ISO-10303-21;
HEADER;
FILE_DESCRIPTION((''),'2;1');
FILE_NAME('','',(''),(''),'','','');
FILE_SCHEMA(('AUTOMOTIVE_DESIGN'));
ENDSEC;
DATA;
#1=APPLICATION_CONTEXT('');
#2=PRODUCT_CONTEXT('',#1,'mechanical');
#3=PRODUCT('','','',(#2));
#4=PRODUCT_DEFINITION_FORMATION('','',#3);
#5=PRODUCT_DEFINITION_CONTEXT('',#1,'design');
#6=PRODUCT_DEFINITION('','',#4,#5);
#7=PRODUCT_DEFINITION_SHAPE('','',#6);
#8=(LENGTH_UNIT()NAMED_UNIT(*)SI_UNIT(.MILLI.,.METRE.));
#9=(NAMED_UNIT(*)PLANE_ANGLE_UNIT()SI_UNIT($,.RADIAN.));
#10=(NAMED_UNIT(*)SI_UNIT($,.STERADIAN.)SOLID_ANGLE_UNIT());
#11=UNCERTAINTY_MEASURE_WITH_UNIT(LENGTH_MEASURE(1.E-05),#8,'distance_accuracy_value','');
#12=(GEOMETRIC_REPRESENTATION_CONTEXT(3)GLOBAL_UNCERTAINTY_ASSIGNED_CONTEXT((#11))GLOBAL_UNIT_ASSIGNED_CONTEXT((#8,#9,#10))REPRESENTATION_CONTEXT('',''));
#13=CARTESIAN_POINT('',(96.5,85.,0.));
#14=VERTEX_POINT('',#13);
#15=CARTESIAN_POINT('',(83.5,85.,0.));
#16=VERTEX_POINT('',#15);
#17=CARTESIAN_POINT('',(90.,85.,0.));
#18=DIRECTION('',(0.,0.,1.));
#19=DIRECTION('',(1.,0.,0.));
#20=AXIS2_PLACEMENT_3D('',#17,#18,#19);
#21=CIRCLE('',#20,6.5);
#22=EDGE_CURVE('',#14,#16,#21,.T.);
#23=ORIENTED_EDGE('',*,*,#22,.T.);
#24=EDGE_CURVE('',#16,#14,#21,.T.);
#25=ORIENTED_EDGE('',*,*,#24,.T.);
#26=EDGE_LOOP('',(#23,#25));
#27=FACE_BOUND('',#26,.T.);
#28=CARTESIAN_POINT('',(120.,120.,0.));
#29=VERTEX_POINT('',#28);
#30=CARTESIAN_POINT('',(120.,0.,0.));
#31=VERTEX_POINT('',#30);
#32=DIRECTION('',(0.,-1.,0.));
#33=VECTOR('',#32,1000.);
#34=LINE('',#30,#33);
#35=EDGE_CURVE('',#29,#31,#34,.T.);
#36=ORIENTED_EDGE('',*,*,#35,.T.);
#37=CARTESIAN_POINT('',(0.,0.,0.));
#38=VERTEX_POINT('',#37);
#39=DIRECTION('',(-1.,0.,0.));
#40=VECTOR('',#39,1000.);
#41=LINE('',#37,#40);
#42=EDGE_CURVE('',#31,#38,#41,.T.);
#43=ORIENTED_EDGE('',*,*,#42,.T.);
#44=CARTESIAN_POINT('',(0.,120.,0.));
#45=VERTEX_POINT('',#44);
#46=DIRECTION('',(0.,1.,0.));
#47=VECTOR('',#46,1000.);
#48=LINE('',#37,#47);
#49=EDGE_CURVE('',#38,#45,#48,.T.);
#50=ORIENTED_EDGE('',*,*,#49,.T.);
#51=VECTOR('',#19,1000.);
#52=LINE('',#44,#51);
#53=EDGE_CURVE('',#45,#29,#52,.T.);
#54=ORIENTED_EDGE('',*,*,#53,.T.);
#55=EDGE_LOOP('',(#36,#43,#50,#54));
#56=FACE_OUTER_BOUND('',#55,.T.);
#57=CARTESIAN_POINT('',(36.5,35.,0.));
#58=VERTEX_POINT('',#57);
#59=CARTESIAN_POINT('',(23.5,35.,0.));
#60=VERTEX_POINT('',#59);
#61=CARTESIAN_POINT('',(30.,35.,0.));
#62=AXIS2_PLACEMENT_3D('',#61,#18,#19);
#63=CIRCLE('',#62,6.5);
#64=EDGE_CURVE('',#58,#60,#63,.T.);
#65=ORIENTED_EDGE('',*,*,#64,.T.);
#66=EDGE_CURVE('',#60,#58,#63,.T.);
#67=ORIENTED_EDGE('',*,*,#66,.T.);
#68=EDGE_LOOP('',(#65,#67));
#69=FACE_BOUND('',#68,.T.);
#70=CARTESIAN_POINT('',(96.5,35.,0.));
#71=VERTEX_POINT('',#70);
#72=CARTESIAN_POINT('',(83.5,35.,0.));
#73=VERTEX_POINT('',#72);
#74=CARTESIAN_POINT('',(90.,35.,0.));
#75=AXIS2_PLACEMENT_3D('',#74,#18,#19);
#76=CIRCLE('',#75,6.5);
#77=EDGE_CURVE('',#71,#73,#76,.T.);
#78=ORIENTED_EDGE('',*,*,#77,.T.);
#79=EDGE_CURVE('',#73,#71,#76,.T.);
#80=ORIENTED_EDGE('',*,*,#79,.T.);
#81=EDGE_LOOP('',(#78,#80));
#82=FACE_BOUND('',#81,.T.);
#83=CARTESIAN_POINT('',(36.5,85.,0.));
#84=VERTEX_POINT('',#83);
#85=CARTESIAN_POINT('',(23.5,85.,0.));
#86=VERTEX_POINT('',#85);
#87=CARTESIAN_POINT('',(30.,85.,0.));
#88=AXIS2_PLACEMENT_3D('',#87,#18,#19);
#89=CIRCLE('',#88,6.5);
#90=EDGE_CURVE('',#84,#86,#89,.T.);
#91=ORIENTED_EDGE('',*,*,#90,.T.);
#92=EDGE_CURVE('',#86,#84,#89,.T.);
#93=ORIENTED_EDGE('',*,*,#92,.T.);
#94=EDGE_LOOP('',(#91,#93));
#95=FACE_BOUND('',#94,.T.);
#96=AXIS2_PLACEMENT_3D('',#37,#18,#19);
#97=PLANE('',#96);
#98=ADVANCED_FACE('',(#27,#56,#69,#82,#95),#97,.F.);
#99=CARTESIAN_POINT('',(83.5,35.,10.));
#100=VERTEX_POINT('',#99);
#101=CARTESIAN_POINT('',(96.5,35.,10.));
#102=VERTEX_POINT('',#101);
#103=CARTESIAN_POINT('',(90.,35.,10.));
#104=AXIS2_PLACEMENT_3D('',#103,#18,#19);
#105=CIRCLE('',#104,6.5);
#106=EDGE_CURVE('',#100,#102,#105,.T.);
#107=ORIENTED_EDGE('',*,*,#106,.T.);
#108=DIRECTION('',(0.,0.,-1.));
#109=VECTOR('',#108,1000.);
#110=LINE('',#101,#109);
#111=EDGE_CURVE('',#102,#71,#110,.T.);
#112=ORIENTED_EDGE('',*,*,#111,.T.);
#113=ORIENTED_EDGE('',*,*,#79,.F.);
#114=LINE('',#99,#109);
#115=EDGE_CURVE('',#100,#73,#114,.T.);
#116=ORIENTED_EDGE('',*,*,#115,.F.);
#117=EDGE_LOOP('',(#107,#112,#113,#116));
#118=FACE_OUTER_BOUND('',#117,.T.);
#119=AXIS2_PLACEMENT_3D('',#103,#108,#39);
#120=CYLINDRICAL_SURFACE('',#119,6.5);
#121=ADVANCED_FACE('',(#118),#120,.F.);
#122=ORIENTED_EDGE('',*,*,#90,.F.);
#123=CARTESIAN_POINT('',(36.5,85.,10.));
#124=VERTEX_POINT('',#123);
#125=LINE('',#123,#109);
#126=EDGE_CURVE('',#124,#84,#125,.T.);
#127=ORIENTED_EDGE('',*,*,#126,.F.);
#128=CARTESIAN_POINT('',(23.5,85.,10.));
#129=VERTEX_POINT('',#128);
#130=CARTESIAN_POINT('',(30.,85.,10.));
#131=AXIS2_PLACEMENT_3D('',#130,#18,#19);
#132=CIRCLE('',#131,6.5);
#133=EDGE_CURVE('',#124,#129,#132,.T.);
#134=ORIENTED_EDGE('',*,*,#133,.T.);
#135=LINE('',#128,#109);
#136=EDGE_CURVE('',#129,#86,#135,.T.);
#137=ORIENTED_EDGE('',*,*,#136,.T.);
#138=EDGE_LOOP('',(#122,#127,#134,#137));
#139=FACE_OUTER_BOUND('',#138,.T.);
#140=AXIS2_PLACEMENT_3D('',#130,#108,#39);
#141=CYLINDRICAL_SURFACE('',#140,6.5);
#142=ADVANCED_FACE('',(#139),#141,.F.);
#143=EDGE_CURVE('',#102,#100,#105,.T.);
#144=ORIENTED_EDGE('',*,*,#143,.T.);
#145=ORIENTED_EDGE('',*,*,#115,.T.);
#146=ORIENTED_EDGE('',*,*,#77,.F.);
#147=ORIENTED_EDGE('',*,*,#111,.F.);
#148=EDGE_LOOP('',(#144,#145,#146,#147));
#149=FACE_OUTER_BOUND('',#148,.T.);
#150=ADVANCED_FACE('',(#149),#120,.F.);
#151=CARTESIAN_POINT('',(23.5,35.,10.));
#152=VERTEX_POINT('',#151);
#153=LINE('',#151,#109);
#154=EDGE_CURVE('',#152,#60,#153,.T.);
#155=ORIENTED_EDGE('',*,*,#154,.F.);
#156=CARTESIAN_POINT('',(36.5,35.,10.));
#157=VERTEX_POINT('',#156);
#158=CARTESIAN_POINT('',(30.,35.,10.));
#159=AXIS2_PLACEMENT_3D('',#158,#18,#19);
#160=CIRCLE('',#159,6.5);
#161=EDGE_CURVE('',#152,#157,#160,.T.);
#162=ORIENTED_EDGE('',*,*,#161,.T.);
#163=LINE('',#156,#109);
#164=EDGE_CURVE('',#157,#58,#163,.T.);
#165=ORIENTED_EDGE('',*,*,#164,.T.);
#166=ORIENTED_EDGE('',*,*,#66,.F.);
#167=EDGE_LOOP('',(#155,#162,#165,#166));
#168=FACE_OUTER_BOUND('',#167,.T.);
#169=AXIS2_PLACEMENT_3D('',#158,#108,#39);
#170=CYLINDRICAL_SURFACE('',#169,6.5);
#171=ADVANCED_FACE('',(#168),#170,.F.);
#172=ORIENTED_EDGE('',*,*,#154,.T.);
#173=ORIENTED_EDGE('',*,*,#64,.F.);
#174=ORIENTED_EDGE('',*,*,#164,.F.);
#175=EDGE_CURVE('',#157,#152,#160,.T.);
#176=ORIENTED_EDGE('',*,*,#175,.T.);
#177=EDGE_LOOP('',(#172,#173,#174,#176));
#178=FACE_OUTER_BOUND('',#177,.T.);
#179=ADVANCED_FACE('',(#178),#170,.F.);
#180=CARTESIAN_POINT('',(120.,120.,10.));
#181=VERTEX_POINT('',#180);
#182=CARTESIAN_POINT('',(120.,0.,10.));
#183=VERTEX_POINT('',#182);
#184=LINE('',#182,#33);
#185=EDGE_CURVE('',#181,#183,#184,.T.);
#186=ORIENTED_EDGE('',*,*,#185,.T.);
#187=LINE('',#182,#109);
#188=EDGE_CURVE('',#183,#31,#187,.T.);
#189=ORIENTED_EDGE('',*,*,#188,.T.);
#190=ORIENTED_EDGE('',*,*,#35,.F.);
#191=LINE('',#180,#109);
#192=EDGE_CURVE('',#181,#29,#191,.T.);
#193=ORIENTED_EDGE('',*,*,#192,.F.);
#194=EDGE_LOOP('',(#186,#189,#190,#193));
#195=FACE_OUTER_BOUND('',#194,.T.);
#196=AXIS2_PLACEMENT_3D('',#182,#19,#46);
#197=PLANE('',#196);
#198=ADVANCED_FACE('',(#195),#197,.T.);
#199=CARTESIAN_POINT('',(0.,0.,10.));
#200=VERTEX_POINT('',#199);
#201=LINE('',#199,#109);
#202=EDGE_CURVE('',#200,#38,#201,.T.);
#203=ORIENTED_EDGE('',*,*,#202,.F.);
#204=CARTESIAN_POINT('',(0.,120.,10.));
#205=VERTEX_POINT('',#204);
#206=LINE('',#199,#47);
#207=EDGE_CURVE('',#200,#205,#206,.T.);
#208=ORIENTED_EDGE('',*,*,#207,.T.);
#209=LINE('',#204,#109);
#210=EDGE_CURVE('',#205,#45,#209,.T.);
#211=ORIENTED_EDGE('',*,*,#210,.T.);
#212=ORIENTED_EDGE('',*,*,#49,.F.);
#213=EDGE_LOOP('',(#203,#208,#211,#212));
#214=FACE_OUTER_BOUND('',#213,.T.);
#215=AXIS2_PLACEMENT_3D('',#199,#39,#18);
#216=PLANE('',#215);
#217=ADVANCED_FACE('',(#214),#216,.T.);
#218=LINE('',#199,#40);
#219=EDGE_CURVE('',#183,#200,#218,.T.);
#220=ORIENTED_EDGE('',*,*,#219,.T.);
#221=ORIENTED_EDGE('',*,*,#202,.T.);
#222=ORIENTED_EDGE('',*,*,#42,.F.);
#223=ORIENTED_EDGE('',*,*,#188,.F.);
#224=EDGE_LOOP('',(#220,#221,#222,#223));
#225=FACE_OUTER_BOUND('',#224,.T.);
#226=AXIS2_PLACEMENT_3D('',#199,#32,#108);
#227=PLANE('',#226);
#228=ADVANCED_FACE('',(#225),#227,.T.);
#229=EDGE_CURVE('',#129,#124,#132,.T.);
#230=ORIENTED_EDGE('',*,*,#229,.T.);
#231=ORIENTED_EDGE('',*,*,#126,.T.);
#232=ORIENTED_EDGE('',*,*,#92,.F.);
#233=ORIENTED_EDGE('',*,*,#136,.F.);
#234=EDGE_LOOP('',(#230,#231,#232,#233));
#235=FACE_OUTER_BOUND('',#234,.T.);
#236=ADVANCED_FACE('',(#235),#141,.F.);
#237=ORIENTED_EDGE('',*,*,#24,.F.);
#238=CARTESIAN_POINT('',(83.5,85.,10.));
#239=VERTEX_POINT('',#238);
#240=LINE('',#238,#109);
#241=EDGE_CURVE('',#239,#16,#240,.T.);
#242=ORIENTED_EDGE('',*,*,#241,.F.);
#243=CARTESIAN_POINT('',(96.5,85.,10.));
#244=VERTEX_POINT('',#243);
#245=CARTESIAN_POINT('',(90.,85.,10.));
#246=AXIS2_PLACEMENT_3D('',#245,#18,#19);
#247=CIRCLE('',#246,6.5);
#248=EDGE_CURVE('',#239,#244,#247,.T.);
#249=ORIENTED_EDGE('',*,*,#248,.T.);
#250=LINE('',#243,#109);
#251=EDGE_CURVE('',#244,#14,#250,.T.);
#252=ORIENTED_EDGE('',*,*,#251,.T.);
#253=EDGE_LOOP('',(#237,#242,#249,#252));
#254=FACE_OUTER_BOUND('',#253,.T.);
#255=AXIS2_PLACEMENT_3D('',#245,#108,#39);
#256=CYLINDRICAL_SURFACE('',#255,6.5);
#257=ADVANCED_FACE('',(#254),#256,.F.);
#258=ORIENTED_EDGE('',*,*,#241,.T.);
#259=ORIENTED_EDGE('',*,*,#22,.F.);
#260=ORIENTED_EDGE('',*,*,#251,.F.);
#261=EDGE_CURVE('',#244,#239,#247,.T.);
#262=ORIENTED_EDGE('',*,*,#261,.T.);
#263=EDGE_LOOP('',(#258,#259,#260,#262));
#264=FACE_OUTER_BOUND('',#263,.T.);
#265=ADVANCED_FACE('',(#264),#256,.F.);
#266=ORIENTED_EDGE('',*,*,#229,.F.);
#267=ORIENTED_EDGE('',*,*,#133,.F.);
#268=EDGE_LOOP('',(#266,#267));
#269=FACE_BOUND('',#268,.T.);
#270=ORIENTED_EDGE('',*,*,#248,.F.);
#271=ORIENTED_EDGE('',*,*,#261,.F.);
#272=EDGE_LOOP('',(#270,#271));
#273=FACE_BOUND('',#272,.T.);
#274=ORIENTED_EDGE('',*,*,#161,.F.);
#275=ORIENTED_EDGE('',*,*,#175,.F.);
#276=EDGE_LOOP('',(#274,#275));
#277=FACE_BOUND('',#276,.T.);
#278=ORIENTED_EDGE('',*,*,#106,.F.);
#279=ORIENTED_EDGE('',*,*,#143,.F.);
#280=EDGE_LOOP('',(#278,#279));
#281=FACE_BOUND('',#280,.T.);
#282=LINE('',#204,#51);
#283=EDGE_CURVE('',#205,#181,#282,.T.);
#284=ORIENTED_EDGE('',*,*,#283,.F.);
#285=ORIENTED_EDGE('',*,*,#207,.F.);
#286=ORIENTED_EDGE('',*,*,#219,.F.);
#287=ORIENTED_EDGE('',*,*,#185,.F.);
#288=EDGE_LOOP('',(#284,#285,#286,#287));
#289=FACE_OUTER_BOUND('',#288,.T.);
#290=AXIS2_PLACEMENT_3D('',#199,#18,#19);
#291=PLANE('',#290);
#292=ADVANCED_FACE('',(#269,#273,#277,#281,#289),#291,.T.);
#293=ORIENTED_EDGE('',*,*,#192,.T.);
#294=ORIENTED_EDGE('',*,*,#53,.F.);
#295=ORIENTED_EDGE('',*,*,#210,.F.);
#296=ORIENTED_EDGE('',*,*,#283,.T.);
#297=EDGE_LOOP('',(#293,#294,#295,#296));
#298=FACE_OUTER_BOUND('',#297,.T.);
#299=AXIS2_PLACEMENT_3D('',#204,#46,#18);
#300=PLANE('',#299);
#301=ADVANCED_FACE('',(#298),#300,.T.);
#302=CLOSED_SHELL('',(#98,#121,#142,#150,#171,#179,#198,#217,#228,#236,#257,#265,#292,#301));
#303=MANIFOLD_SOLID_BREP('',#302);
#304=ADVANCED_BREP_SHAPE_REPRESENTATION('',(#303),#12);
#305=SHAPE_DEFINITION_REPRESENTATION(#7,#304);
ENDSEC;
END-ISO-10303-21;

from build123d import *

# Parameters (mm, degrees)
SKETCH_1_W      = 120
SKETCH_1_H      = 120
SKETCH_1_R      = 6.5
EXTRUDE_1_DEPTH = 10


with BuildPart() as part:
    # 草图1 → 凸台-拉伸1 (new body)
    with BuildSketch(Plane.XY):
        with Locations((60, 60)):
            Rectangle(SKETCH_1_W, SKETCH_1_H)
        with Locations((90, 35)):
            Circle(SKETCH_1_R, mode=Mode.SUBTRACT)
        with Locations((30, 85)):
            Circle(SKETCH_1_R, mode=Mode.SUBTRACT)
        with Locations((90, 85)):
            Circle(SKETCH_1_R, mode=Mode.SUBTRACT)
        with Locations((30, 35)):
            Circle(SKETCH_1_R, mode=Mode.SUBTRACT)
    extrude(amount=EXTRUDE_1_DEPTH)


solid = part.part
